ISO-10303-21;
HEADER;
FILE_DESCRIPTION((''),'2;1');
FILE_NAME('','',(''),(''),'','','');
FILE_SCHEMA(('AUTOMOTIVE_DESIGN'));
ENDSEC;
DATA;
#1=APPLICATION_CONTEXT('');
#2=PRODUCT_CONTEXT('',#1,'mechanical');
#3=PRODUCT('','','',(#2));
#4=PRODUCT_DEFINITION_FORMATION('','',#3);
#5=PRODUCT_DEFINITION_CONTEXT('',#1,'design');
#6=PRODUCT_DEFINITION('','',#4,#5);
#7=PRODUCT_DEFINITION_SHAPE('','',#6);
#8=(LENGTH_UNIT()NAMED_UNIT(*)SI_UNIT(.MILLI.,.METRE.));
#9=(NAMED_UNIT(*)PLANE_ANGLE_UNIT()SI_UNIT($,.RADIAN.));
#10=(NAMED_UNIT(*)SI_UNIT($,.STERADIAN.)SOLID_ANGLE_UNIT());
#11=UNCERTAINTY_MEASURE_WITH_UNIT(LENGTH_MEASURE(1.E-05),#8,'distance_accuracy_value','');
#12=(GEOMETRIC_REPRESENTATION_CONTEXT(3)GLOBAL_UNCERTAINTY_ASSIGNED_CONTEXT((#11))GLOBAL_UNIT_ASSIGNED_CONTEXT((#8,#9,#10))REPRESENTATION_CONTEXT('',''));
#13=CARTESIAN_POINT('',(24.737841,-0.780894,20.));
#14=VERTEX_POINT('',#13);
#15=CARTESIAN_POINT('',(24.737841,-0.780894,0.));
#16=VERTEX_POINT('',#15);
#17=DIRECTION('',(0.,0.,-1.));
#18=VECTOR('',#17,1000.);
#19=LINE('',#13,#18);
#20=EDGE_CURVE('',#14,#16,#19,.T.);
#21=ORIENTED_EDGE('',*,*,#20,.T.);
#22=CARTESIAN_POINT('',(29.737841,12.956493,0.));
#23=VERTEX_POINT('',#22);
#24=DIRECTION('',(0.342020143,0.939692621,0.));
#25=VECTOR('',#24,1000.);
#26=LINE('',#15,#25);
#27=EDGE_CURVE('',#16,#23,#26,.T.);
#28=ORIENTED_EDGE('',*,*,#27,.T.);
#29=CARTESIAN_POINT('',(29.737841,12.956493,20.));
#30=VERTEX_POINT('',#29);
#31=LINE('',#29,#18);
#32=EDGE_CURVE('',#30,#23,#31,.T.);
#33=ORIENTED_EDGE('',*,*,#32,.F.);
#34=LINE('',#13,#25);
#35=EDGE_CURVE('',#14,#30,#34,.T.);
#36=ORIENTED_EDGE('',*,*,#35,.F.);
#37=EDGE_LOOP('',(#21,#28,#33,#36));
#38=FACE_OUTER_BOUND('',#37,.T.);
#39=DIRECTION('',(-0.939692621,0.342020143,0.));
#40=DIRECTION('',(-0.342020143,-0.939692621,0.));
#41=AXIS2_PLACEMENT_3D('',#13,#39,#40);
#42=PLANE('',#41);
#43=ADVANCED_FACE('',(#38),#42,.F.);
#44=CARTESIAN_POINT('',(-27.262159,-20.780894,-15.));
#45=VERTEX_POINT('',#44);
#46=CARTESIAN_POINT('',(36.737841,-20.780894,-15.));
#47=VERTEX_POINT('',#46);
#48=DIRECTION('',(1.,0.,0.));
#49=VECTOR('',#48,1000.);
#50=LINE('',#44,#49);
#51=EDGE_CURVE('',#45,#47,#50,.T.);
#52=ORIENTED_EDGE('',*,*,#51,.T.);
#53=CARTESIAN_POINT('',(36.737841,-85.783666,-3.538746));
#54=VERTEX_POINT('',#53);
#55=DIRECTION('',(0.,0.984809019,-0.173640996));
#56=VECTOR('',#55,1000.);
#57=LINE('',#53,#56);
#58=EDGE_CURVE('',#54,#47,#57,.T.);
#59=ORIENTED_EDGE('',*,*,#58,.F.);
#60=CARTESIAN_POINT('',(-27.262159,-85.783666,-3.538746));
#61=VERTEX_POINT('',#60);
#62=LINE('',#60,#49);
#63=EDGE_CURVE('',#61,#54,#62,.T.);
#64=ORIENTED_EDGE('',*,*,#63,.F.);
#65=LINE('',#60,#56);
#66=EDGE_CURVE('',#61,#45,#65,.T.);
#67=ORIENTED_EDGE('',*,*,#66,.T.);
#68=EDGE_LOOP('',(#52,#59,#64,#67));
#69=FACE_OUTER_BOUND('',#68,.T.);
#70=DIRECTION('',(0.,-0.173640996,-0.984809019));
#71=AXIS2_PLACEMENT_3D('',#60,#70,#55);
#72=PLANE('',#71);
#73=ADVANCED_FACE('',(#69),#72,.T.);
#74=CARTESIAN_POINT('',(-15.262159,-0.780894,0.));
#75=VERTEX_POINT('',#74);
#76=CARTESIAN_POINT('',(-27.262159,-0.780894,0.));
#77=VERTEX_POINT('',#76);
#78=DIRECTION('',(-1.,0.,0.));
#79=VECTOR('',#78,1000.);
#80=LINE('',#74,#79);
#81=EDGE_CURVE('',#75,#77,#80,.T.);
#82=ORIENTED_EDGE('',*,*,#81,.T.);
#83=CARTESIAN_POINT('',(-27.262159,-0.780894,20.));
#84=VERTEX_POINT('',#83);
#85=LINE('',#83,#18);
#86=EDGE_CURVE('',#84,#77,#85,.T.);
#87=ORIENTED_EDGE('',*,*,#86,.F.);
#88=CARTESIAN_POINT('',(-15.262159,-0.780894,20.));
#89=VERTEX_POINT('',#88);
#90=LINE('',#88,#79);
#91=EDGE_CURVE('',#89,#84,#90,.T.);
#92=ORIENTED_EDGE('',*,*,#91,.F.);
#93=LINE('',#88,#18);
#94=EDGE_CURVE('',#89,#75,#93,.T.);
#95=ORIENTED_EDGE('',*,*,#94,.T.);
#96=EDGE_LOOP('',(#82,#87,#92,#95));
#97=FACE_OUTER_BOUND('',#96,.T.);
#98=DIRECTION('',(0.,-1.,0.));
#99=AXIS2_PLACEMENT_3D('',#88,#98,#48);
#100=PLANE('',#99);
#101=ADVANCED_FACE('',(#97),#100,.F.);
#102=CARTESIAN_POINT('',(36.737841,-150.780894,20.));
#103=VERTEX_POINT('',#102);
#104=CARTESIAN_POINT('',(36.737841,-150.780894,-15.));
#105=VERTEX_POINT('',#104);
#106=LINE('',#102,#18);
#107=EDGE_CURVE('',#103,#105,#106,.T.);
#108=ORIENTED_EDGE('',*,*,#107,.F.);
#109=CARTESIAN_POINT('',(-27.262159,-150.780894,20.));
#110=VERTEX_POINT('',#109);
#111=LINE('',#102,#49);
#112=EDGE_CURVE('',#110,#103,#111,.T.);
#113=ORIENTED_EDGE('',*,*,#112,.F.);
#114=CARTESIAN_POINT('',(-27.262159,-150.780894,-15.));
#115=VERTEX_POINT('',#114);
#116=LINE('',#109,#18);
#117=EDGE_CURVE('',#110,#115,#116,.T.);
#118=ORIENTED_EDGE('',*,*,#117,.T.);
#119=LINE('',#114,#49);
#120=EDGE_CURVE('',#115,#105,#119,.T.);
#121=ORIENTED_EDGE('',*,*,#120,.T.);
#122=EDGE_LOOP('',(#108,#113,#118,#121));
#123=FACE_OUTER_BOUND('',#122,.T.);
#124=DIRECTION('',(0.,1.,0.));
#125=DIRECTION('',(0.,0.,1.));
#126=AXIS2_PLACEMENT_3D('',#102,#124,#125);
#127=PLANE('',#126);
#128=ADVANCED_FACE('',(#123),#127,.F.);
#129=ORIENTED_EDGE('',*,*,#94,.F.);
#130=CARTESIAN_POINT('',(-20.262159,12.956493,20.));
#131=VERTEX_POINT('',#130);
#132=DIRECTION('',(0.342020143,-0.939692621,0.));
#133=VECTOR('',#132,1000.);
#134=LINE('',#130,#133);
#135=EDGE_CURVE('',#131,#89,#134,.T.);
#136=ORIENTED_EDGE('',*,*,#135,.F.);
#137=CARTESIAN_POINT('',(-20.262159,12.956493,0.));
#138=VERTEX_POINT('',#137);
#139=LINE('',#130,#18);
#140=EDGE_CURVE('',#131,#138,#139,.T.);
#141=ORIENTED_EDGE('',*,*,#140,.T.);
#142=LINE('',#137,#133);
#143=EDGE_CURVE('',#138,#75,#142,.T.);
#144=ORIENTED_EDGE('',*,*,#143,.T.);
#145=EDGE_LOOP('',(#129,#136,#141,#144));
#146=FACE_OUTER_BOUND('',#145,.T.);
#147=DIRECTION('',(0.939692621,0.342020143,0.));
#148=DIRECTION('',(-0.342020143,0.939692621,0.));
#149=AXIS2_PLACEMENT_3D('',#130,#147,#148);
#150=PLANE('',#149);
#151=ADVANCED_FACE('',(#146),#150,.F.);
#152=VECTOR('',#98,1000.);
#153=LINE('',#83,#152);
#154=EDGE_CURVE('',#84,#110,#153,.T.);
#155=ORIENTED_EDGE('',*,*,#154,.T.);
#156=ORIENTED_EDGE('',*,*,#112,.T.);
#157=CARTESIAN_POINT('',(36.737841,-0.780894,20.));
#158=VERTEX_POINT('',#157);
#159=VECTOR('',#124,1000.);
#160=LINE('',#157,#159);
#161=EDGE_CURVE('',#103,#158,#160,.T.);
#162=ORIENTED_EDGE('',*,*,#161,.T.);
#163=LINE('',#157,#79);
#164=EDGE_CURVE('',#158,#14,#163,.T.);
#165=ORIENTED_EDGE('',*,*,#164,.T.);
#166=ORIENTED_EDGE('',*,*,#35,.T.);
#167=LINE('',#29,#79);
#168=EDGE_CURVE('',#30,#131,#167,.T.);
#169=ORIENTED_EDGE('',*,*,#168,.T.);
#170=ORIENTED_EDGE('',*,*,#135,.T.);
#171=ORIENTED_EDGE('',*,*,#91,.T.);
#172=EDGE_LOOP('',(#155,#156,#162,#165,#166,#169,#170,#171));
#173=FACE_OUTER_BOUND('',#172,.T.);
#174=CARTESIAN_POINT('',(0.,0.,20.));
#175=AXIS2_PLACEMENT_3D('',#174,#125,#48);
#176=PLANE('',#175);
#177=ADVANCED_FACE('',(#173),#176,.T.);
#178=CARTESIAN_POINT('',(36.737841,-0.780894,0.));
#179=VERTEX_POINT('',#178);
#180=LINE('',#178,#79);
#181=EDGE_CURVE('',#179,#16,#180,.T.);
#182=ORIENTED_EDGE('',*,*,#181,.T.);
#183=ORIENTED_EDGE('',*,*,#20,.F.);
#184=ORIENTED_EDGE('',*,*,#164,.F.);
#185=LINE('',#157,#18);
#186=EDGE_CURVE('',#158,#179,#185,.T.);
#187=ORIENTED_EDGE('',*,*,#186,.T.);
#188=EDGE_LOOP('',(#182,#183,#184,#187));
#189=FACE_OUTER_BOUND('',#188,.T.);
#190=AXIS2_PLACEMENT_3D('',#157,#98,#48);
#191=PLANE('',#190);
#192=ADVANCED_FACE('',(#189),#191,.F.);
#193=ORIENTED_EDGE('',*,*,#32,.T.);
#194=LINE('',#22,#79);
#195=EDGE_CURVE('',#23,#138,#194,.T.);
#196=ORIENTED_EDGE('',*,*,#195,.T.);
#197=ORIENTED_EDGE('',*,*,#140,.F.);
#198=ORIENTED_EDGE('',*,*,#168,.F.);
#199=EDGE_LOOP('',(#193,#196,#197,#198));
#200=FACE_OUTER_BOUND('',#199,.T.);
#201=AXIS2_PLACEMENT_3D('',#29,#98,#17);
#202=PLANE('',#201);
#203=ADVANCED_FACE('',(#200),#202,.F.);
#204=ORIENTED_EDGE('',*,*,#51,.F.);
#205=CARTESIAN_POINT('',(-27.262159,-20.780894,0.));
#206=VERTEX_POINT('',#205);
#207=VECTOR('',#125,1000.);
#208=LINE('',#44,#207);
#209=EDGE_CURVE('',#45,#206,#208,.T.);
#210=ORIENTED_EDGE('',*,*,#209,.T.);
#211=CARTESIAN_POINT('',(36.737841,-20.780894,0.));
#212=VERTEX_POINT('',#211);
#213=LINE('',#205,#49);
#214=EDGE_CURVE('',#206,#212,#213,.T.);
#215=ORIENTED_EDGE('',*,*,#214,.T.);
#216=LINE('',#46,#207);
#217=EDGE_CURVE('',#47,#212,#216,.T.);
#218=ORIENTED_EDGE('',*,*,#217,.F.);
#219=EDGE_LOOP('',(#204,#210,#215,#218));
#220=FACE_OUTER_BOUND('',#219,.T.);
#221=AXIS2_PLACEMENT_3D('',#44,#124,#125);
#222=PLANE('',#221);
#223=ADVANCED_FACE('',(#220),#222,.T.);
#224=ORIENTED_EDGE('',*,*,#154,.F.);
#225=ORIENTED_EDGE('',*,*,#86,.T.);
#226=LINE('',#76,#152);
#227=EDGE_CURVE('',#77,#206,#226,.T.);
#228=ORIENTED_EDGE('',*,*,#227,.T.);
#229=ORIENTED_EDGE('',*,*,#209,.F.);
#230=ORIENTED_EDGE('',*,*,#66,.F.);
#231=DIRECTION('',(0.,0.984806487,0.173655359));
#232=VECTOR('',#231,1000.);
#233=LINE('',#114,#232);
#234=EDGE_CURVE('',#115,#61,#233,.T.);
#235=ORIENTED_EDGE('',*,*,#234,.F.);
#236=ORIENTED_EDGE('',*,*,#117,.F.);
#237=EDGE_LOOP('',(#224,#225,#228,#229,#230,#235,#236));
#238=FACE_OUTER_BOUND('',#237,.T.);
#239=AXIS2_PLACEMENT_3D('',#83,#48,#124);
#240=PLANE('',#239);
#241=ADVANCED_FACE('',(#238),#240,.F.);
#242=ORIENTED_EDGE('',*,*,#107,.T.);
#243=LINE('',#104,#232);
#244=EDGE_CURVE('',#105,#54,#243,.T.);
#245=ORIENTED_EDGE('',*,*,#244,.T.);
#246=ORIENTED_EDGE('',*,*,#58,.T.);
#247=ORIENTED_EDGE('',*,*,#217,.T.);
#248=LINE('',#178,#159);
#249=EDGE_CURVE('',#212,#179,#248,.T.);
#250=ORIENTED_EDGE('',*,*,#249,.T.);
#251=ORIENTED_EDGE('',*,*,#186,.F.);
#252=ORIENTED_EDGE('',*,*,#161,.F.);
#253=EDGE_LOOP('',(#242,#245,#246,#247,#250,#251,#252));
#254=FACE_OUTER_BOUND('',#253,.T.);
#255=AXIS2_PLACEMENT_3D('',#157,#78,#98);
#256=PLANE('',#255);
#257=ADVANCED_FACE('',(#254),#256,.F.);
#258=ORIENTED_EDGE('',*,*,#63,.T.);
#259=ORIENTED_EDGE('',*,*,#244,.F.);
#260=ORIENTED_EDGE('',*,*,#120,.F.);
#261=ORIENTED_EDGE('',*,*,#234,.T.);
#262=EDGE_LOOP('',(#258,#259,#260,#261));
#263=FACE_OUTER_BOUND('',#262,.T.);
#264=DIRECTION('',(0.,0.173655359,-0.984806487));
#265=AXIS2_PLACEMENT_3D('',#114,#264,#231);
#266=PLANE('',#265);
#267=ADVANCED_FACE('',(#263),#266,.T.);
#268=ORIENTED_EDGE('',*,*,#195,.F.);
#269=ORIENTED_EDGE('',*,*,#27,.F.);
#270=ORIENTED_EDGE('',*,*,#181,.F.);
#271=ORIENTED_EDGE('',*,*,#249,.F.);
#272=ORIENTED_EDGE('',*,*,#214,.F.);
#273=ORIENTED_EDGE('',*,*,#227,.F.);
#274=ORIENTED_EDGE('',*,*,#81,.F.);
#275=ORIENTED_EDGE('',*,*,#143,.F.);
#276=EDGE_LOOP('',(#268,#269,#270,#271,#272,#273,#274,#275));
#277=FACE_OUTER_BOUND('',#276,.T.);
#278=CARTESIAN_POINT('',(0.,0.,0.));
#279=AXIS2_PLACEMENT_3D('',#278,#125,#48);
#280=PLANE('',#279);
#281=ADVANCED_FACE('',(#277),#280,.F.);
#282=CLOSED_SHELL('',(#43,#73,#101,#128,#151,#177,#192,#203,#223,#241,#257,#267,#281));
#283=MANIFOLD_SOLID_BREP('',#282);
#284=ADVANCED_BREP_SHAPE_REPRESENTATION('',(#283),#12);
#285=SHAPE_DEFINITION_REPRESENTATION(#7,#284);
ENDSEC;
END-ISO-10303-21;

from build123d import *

# Parameters (mm, degrees)
BOSS_EXTRUDE1_DEPTH = 20
BOSS_EXTRUDE2_DEPTH = 64


with BuildPart() as part:
    # Sketch1 → Boss-Extrude1 (new body)
    with BuildSketch(Plane.XY):
        Polygon((-27.262159038, -0.780894157), (-27.262159038, -150.780894157), (36.737840962, -150.780894157), (36.737840962, -0.780894157), (24.737840962, -0.780894157), (29.737840962, 12.95649294), (-20.262159038, 12.95649294), (-15.262159038, -0.780894157), align=None)
    extrude(amount=BOSS_EXTRUDE1_DEPTH)

    # Sketch2 → Boss-Extrude2 (add)
    with BuildSketch(Plane(origin=(36.737840962, 0, 0), x_dir=(0, 0, -1), z_dir=(1, 0, 0))):
        Polygon((0, -150.780894157), (15, -150.780894157), (3.538746274, -85.783666039), (15, -20.780894157), (0, -20.780894157), align=None)
    extrude(amount=-BOSS_EXTRUDE2_DEPTH)


solid = part.part
